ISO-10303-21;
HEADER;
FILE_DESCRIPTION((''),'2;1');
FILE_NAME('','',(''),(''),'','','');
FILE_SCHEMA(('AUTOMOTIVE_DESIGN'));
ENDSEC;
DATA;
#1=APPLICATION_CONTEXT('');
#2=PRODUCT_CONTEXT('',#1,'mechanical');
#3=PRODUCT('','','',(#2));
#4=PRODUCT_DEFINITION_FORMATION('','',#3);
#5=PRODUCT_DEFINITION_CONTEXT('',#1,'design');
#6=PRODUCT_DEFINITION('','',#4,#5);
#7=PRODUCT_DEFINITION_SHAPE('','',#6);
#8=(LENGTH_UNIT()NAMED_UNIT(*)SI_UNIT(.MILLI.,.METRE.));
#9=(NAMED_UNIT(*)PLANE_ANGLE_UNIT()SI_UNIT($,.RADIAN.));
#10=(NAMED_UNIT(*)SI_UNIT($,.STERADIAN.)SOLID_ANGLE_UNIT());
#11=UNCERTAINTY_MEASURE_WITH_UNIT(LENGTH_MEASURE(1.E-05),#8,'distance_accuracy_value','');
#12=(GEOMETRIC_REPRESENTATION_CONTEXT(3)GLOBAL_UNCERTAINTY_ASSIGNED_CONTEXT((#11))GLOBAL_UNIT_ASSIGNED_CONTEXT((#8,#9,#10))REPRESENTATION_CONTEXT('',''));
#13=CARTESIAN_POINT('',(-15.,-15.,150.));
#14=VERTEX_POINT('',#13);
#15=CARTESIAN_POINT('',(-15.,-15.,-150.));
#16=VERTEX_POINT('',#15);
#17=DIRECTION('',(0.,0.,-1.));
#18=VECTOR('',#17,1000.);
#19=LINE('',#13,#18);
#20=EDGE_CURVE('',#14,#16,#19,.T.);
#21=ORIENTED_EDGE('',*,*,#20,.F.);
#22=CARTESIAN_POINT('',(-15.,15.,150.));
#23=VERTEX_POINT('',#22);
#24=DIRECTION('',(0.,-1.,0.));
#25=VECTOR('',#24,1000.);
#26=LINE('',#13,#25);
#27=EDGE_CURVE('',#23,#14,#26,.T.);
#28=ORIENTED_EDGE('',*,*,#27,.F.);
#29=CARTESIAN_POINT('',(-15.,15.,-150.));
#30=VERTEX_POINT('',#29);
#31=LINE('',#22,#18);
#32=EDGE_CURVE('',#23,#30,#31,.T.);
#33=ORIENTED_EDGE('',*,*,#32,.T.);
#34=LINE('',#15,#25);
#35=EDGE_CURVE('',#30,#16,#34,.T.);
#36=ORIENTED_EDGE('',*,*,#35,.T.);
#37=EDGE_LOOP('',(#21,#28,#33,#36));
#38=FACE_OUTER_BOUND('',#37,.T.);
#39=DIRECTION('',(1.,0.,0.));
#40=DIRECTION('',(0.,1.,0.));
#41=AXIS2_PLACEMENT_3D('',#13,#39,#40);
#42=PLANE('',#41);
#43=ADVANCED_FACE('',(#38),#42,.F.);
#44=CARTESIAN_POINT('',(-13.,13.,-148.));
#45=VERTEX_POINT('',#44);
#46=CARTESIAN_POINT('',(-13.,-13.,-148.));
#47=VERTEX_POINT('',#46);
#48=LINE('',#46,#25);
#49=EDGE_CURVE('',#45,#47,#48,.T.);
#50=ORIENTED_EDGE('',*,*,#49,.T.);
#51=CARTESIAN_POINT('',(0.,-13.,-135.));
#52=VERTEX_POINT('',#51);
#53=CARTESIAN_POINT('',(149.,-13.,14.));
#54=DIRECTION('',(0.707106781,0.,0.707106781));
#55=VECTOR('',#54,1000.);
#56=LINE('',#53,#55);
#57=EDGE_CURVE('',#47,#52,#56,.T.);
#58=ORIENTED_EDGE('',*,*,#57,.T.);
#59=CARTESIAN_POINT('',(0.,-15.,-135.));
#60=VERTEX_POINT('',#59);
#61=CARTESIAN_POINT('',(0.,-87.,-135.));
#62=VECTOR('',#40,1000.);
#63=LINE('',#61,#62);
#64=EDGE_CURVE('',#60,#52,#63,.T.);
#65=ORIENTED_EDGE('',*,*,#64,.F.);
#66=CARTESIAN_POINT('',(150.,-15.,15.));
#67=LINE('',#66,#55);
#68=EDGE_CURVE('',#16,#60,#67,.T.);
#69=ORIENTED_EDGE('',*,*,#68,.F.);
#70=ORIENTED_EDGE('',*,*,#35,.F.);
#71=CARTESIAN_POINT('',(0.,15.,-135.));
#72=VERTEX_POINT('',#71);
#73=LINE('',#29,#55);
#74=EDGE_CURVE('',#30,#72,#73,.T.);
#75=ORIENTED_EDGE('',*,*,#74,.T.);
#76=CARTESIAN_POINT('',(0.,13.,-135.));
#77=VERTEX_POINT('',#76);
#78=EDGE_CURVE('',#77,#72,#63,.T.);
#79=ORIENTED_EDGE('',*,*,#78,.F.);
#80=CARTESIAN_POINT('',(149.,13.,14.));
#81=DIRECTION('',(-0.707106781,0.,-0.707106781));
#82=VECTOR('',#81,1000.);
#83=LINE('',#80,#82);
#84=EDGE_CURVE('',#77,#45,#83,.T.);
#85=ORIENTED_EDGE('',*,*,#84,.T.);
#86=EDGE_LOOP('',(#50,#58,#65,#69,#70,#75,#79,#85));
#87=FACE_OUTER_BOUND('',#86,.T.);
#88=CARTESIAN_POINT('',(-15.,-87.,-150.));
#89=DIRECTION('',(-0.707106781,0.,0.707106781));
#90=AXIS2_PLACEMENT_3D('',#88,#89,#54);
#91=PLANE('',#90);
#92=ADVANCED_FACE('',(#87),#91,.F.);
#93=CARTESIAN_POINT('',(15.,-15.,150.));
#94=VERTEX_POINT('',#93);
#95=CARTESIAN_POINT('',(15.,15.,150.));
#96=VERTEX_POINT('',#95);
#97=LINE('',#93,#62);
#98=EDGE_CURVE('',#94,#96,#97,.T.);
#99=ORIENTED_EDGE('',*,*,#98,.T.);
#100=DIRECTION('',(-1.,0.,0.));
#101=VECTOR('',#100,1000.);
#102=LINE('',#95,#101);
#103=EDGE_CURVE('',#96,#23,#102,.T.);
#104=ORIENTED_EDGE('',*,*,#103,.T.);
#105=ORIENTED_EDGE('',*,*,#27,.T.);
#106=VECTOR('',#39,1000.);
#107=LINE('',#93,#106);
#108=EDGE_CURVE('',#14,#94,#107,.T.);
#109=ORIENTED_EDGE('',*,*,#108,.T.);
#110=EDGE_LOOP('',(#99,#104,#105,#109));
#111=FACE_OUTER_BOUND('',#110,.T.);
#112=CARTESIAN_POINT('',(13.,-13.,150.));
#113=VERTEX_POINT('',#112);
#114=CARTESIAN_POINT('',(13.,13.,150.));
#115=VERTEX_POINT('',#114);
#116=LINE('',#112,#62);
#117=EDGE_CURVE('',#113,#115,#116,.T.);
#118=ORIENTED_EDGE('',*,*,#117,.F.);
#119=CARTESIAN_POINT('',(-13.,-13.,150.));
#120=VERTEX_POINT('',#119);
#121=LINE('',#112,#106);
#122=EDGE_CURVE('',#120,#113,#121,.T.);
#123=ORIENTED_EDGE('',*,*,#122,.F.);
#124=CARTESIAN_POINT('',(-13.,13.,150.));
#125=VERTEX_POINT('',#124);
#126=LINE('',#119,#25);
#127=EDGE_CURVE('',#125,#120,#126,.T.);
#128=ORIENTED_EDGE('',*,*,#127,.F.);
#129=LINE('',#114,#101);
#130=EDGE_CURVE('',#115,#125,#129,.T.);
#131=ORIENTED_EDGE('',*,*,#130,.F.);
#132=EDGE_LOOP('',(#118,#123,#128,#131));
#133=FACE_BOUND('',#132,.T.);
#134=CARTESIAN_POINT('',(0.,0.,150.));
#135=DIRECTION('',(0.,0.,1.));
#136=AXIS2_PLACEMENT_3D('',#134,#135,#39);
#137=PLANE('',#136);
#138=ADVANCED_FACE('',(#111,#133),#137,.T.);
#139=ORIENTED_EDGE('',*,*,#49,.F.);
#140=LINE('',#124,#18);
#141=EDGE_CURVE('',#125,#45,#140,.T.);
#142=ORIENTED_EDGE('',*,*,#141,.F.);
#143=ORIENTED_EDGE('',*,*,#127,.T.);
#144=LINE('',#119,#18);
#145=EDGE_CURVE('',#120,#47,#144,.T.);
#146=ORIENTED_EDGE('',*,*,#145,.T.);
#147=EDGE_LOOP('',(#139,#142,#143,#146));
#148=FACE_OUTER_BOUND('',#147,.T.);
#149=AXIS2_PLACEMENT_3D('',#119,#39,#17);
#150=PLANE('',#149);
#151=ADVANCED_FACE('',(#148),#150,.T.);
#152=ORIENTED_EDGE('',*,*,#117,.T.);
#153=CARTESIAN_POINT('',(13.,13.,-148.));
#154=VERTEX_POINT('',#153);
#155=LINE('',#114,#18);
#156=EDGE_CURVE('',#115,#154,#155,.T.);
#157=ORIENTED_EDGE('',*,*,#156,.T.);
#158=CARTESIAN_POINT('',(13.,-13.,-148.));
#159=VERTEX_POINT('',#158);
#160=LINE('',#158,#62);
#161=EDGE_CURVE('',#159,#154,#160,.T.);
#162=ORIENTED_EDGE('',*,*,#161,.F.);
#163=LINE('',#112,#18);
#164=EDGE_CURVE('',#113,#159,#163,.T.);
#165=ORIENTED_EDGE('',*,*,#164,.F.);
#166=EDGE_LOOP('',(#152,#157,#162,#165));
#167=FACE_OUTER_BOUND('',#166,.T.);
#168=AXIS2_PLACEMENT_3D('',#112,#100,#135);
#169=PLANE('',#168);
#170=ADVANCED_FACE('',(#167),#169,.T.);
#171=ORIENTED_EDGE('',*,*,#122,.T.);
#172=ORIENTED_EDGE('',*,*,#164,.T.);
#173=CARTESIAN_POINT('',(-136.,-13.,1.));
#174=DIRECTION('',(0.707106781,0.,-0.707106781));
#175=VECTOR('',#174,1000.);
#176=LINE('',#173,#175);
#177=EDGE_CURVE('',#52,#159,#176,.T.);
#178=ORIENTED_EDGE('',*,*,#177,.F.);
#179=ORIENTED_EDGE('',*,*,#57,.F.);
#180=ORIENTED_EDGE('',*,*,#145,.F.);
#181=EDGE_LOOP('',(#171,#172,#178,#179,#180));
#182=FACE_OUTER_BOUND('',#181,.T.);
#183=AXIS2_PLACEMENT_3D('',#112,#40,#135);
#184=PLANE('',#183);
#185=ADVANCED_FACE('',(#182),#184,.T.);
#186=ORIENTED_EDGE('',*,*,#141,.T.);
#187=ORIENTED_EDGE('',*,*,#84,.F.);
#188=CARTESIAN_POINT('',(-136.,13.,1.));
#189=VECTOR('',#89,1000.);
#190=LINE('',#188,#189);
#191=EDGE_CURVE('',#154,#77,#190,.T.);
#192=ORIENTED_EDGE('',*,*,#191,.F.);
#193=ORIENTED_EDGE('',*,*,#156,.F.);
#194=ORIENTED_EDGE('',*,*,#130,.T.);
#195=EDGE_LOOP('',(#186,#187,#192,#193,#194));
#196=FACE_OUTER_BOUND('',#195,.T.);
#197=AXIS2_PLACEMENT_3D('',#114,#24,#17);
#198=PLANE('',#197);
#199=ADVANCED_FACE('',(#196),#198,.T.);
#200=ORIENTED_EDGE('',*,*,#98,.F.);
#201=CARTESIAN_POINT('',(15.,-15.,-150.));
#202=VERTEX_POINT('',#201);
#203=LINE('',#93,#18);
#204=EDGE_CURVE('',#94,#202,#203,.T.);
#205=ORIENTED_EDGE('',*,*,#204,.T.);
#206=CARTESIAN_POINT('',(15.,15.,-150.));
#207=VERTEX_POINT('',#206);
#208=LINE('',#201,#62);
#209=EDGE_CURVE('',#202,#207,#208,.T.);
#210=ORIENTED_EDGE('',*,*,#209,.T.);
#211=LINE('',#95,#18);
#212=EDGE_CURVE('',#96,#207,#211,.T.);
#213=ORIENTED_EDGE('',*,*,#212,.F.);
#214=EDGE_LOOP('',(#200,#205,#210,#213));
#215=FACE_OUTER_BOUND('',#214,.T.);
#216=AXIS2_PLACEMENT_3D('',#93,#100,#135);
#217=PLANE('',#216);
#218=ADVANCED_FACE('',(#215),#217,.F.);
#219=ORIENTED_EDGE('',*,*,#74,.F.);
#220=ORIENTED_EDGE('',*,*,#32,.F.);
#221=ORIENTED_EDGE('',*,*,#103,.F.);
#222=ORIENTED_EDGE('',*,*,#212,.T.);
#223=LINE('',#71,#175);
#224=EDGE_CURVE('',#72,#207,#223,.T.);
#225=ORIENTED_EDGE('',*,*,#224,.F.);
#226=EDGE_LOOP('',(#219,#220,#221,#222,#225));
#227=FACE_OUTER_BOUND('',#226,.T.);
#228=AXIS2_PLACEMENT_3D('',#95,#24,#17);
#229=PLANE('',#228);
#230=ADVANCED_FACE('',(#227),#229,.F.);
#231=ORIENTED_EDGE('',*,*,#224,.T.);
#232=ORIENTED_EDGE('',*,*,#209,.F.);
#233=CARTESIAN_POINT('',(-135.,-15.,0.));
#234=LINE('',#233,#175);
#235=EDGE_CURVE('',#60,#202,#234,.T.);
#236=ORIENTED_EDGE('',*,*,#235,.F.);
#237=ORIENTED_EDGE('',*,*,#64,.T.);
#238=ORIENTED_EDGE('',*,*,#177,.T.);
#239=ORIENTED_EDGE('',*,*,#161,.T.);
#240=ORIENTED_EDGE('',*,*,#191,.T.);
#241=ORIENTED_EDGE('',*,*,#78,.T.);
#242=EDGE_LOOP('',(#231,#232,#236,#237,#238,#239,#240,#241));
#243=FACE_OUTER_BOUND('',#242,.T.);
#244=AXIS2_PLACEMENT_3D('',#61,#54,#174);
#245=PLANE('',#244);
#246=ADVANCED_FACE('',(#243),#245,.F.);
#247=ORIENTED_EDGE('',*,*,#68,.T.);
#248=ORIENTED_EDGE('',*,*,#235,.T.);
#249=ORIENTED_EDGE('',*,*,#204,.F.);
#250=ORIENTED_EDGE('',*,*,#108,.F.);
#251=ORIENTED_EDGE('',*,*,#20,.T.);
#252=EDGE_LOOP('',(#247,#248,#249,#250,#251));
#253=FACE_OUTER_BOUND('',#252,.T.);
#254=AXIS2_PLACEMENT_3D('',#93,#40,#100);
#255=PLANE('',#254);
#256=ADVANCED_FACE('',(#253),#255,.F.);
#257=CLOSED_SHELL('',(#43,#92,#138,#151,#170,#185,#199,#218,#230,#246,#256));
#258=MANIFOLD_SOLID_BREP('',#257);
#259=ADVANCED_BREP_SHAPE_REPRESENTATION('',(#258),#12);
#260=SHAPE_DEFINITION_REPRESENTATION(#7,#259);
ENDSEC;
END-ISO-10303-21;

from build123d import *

# Parameters (mm, degrees)
SKETCH_1_W          = 30
SKETCH_1_H          = 30
SKETCH_1_W_2        = 26
SKETCH_1_H_2        = 26
EXTRUDE_1_DEPTH     = 150
CUT_EXTRUDE_1_DEPTH = 102


with BuildPart() as part:
    # 草图1 → 凸台-拉伸1 (new, symmetric)
    with BuildSketch(Plane.XY):
        Rectangle(SKETCH_1_W, SKETCH_1_H)
        Rectangle(SKETCH_1_W_2, SKETCH_1_H_2, mode=Mode.SUBTRACT)
    extrude(amount=EXTRUDE_1_DEPTH, both=True)

    # 草图3 → 切除-拉伸1 (cut)
    with BuildSketch(Plane(origin=(0, 15, 0), x_dir=(1, 0, 0), z_dir=(0, 1, 0))):
        Polygon((-15, 150), (0, 135), (15, 150), align=None)
    extrude(amount=-CUT_EXTRUDE_1_DEPTH, mode=Mode.SUBTRACT)


solid = part.part
